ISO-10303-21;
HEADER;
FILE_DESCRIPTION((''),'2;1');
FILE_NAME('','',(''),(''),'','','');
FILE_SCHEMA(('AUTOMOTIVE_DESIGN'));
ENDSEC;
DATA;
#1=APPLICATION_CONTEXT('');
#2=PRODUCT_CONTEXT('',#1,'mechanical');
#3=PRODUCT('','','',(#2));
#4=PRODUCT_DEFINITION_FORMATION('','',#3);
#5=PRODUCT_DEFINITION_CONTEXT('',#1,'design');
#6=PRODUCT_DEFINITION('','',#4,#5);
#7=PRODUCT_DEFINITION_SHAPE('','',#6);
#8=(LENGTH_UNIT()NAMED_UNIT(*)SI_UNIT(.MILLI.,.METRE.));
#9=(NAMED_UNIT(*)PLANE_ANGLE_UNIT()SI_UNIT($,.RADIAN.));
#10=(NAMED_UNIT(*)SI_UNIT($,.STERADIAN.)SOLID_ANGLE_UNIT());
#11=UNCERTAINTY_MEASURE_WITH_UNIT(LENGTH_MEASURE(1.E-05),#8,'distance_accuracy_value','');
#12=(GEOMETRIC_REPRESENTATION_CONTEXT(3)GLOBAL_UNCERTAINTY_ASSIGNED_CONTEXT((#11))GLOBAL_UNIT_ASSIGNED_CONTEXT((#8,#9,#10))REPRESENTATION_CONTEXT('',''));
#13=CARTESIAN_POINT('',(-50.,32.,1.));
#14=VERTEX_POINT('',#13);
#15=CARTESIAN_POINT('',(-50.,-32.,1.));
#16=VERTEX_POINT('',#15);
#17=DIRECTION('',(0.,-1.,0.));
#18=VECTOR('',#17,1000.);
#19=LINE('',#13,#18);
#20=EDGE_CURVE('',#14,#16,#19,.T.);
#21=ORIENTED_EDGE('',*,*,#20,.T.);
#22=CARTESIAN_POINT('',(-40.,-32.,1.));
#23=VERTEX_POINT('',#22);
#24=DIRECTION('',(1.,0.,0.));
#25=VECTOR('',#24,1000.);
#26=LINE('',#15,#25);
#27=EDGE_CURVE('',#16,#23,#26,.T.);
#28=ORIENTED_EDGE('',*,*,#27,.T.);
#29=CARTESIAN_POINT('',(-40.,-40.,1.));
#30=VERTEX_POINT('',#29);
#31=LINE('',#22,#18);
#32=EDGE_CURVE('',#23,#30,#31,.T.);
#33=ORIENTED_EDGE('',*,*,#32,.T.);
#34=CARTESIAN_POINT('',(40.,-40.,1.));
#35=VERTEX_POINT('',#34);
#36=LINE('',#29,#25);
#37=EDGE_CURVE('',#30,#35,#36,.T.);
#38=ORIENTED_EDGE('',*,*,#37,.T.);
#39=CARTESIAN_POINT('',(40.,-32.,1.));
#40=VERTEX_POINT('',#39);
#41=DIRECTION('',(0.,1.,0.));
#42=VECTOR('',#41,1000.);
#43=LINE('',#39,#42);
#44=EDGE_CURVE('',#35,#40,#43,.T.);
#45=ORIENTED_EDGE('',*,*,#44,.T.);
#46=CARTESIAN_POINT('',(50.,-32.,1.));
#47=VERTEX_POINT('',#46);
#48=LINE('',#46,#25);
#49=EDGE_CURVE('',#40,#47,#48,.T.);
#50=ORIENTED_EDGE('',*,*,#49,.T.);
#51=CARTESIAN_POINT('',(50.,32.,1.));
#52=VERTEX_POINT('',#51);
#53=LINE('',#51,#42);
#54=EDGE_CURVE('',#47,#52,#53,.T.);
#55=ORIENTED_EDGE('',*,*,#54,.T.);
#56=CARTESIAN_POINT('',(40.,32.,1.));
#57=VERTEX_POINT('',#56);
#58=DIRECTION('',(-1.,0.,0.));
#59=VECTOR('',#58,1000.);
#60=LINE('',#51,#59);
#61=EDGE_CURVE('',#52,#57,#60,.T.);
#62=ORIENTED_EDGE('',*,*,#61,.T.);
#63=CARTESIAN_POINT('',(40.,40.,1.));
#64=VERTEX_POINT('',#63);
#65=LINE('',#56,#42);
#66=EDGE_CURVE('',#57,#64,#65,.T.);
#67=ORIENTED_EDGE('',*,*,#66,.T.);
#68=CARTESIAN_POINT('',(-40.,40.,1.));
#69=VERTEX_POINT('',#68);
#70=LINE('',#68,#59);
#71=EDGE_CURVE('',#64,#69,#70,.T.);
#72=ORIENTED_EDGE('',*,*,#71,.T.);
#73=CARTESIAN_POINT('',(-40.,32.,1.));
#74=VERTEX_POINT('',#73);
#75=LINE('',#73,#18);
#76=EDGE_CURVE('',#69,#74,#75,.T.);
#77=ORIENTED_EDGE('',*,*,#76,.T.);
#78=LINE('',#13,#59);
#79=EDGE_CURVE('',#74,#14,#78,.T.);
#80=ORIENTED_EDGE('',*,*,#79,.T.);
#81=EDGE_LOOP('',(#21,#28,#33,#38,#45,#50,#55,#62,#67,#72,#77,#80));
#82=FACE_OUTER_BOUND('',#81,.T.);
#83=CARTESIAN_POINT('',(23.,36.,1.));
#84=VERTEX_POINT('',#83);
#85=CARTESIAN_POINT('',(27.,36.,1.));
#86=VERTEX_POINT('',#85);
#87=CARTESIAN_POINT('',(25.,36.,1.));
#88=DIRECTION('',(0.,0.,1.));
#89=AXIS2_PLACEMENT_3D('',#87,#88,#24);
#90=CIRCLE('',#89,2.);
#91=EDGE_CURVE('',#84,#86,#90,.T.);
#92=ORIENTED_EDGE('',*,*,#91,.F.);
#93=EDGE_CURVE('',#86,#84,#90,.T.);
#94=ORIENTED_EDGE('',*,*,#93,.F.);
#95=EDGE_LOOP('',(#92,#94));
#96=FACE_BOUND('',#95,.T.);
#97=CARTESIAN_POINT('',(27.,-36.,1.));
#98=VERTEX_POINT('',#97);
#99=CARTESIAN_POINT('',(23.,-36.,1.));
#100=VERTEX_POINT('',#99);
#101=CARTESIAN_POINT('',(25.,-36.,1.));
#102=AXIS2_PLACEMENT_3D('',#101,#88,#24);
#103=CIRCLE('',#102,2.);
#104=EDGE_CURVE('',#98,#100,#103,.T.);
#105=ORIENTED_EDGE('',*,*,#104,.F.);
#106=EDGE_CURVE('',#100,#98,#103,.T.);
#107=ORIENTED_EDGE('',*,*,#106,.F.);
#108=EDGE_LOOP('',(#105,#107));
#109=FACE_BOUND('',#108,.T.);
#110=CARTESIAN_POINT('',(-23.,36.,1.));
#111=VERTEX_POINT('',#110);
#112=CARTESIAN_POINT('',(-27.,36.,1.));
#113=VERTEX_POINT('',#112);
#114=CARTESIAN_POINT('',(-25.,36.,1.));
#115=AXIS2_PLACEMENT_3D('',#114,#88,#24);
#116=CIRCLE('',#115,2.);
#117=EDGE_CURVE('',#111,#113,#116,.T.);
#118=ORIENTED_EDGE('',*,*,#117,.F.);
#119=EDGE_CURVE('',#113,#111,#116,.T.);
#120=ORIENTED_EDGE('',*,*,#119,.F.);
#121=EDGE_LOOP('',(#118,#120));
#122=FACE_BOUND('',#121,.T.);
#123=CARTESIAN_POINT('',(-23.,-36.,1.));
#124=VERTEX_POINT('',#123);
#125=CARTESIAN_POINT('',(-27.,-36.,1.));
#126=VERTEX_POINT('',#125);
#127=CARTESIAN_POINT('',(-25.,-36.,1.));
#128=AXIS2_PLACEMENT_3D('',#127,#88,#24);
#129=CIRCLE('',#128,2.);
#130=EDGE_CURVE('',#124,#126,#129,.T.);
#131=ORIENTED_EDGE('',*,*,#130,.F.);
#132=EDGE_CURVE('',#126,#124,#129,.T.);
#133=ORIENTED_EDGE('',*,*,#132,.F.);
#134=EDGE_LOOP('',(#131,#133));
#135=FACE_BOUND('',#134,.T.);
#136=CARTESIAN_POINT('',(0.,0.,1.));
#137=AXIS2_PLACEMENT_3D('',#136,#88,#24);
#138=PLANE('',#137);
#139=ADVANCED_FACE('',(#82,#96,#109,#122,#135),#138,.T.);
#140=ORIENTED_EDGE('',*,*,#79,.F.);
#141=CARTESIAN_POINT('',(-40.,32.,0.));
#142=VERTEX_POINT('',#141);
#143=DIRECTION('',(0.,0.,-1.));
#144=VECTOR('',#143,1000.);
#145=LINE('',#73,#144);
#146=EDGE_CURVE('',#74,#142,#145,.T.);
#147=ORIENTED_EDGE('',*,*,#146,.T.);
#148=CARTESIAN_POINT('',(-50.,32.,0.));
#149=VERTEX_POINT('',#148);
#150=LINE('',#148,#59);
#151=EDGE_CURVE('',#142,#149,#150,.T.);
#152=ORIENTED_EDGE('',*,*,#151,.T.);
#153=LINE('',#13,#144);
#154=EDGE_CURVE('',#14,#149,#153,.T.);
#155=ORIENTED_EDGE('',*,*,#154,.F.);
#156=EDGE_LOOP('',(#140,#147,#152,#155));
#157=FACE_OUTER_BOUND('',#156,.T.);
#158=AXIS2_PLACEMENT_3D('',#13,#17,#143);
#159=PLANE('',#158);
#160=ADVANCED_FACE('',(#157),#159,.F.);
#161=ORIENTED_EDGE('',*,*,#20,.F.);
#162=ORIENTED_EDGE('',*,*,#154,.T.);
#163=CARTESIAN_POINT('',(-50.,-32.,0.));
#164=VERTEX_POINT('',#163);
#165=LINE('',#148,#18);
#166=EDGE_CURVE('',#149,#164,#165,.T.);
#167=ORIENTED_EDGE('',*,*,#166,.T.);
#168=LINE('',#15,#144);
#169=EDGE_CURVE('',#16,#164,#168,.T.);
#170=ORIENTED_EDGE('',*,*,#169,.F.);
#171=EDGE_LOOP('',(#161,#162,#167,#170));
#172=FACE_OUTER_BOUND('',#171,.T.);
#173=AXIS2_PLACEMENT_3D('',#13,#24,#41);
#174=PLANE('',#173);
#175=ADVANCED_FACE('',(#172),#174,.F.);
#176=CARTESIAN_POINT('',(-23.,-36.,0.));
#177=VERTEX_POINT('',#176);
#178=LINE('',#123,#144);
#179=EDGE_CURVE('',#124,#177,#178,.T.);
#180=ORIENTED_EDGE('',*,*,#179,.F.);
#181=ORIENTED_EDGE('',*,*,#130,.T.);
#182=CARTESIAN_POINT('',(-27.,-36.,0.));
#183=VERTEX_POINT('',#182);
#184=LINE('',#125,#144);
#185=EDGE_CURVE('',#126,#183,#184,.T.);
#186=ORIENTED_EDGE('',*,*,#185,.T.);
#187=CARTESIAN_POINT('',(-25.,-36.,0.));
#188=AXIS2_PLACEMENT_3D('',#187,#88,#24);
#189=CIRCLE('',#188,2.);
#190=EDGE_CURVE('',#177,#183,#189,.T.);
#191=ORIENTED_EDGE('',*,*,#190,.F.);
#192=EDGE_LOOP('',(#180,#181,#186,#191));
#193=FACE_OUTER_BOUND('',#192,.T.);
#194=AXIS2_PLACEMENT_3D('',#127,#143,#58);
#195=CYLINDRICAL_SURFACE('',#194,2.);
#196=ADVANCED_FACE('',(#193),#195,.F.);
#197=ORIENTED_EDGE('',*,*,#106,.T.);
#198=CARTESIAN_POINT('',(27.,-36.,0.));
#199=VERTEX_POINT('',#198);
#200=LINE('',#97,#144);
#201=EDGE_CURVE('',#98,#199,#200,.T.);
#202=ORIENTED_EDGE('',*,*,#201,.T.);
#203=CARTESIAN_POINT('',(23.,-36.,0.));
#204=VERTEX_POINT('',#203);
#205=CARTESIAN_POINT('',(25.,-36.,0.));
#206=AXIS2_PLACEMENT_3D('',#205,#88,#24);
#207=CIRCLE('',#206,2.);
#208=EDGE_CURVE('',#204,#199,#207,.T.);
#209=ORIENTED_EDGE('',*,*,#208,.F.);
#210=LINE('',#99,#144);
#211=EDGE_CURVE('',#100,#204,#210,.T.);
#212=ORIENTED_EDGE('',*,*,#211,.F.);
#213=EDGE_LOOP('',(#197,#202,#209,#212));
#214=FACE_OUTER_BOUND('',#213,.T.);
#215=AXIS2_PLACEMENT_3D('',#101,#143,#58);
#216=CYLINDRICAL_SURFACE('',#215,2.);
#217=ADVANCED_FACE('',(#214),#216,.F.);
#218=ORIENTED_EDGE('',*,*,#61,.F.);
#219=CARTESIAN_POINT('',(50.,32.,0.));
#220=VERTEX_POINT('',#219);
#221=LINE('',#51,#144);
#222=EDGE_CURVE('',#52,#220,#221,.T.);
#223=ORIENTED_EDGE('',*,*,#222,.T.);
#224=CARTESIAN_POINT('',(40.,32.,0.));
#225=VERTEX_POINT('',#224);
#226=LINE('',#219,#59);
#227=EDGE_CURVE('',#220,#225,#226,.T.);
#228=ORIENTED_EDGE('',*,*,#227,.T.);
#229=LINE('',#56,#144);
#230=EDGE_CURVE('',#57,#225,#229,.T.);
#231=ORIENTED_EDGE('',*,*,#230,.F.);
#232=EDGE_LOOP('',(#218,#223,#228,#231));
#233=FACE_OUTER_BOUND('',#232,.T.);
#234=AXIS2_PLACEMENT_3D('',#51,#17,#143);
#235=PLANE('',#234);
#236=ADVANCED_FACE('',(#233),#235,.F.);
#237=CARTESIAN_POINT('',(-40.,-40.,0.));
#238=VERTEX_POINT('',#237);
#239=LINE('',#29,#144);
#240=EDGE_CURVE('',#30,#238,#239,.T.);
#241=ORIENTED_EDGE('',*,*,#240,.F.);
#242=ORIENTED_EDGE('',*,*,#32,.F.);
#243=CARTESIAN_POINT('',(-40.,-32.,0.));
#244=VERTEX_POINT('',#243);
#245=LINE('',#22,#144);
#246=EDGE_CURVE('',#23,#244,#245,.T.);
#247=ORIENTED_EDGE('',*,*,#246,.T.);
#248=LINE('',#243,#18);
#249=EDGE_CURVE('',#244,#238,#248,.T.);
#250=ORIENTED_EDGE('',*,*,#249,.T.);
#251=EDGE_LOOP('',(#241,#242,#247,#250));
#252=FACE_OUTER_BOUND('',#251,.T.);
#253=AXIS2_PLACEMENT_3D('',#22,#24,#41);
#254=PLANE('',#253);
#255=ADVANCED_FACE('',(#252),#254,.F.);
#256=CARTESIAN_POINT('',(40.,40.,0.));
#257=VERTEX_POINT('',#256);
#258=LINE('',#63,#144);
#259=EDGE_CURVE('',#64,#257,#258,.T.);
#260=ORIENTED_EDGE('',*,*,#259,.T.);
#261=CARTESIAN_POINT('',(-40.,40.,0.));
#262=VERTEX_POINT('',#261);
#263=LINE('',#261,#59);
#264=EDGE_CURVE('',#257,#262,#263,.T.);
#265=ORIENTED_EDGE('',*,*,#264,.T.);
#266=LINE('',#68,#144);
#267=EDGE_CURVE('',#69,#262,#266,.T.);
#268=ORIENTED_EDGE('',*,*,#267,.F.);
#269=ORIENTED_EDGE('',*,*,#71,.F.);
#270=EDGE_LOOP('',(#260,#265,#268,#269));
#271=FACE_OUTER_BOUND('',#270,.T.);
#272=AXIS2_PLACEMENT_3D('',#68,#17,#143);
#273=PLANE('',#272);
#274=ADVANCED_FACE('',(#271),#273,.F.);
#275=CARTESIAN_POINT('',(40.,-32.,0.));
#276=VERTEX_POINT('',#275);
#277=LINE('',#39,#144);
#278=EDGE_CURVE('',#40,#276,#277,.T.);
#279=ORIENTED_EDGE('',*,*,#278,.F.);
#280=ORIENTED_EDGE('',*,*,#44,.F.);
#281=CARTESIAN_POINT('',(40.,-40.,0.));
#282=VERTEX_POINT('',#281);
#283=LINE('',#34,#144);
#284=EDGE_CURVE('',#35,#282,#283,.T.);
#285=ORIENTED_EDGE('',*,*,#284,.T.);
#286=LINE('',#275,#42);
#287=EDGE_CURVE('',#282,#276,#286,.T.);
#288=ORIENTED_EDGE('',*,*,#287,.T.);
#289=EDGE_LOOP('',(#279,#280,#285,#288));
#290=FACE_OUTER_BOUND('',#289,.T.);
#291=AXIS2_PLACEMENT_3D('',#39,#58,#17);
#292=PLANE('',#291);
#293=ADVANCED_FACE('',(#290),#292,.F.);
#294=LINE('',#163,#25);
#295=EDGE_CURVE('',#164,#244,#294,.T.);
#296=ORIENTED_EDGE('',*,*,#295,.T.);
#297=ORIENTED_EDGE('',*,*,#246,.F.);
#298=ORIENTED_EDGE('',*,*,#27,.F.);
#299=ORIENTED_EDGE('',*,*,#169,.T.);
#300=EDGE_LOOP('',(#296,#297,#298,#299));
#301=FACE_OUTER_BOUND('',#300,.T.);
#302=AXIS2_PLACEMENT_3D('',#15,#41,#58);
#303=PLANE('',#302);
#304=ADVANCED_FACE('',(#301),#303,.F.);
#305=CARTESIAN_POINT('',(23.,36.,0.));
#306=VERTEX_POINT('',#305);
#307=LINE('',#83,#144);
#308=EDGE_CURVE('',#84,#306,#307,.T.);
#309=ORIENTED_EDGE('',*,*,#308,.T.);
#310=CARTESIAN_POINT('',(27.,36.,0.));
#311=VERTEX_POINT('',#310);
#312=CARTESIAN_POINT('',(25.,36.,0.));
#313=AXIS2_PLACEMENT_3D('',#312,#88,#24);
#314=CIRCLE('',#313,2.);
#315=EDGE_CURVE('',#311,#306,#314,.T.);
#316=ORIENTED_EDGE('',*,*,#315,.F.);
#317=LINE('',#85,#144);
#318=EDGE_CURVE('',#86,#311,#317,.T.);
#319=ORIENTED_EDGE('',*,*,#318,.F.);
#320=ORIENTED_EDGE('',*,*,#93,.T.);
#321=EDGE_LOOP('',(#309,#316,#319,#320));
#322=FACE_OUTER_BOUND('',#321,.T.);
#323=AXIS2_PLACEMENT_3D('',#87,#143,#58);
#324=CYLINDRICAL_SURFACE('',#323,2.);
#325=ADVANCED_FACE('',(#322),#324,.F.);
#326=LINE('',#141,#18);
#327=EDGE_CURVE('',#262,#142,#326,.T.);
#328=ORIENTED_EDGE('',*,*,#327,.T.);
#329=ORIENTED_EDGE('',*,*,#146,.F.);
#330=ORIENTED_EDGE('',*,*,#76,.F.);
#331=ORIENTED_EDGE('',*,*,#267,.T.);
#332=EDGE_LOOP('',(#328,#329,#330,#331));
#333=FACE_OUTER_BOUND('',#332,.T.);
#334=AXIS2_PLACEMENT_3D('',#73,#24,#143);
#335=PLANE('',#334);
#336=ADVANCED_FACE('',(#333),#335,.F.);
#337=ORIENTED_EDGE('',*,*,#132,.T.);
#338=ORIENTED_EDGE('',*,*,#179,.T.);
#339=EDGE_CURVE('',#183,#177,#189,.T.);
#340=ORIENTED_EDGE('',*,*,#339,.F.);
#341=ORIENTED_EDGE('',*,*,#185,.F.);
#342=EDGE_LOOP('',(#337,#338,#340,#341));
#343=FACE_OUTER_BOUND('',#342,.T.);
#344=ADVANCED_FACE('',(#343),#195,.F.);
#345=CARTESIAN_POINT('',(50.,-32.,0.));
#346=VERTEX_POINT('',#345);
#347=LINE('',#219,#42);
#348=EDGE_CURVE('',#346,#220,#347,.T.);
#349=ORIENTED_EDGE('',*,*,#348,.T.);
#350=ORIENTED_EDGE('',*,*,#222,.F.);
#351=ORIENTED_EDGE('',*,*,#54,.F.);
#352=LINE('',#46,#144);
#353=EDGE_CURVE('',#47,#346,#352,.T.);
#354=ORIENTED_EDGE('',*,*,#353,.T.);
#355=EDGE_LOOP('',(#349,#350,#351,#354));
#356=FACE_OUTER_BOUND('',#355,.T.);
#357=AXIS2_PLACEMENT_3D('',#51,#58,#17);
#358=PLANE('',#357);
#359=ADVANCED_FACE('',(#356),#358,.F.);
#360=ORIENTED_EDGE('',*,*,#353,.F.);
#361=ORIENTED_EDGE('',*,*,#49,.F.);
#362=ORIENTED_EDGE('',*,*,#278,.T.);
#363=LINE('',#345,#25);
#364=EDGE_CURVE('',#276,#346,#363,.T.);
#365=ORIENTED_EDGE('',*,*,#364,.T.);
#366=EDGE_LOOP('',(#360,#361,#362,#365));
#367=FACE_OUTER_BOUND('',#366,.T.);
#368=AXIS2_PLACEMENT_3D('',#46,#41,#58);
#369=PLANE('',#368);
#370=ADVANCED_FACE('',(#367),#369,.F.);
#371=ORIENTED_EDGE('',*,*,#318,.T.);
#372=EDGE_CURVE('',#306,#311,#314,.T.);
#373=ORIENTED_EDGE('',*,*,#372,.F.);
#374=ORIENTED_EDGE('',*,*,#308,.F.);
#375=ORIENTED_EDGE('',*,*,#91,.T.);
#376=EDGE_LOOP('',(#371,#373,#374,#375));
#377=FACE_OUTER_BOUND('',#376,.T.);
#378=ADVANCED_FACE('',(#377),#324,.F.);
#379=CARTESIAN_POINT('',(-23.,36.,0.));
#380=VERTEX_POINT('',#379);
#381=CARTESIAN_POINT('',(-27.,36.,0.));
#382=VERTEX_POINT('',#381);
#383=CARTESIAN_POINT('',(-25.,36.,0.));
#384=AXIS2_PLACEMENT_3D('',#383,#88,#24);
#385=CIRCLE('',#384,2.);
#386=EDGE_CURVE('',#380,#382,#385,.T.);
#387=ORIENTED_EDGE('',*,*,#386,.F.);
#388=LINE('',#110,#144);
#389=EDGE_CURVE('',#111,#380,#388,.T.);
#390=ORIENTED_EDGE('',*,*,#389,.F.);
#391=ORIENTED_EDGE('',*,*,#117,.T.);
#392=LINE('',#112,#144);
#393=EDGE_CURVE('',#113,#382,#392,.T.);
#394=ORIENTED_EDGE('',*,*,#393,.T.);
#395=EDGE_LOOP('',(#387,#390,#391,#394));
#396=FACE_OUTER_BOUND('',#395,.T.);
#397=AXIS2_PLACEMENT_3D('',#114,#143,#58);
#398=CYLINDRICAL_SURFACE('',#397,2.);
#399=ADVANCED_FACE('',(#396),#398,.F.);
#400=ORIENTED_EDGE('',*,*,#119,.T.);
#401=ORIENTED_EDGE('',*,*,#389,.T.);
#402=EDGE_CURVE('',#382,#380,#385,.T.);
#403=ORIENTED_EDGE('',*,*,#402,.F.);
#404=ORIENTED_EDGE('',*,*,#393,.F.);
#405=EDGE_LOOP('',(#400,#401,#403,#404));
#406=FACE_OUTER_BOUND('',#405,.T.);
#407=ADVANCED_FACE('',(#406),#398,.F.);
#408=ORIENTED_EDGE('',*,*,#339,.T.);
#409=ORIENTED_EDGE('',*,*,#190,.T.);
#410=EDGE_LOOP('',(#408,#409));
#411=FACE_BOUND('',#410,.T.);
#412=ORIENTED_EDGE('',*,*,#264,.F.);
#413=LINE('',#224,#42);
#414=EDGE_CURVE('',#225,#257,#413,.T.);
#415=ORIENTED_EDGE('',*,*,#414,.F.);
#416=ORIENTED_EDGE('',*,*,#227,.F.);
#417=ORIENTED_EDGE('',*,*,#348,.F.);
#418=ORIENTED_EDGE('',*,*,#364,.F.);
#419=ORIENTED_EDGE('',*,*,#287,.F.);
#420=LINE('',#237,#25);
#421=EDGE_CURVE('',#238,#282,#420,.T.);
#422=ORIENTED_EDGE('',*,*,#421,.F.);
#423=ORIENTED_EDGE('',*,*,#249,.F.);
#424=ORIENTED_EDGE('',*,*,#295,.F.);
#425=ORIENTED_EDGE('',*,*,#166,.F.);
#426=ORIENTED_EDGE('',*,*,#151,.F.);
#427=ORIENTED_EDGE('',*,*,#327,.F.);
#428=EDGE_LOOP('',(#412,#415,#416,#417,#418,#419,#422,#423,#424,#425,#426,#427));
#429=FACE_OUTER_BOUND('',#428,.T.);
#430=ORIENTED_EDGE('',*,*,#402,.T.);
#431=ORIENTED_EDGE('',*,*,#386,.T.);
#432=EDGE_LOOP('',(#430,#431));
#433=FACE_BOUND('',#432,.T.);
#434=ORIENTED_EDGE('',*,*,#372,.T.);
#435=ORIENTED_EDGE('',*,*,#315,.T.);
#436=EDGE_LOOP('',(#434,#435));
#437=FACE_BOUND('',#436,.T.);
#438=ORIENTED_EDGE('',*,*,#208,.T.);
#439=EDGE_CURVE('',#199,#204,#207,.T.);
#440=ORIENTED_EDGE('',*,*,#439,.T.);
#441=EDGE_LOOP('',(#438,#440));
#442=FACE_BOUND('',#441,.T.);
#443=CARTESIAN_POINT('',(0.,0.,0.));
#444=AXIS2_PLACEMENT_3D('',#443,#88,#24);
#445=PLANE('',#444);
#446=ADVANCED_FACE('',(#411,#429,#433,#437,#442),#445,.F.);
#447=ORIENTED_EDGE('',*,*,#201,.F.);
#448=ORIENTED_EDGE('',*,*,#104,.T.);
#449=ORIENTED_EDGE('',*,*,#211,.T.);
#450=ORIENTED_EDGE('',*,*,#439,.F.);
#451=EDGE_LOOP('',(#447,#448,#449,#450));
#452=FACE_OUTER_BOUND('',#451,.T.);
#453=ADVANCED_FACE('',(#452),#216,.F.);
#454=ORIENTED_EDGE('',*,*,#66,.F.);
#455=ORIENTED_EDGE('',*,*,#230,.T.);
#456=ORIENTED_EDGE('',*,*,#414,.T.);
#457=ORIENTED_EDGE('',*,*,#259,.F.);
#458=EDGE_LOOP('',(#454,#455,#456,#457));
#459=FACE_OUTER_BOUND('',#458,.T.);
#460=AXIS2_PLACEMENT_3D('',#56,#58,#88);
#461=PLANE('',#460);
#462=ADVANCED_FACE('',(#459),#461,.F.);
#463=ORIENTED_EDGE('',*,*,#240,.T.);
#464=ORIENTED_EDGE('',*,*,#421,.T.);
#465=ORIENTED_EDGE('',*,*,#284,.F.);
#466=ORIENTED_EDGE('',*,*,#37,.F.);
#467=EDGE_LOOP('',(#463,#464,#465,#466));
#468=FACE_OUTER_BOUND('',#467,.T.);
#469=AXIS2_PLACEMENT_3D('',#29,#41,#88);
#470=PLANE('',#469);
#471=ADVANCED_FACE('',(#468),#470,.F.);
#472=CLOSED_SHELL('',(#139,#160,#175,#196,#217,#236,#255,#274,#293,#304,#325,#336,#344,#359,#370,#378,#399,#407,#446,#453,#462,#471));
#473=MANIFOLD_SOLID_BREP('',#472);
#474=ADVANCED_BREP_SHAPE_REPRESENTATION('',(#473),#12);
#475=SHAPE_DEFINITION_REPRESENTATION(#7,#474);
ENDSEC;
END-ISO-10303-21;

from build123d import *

# Parameters (mm, degrees)
SKETCH1_R           = 2
BOSS_EXTRUDE1_DEPTH = 1


with BuildPart() as part:
    # Sketch1 → Boss-Extrude1 (new body)
    with BuildSketch(Plane.XY):
        Polygon((-40, 40), (40, 40), (40, 32), (50, 32), (50, -32), (40, -32), (40, -40), (-40, -40), (-40, -32), (-50, -32), (-50, 32), (-40, 32), align=None)
        with Locations((-25, 36)):
            Circle(SKETCH1_R, mode=Mode.SUBTRACT)
        with Locations((-25, -36)):
            Circle(SKETCH1_R, mode=Mode.SUBTRACT)
        with Locations((25, 36)):
            Circle(SKETCH1_R, mode=Mode.SUBTRACT)
        with Locations((25, -36)):
            Circle(SKETCH1_R, mode=Mode.SUBTRACT)
    extrude(amount=BOSS_EXTRUDE1_DEPTH)


solid = part.part
